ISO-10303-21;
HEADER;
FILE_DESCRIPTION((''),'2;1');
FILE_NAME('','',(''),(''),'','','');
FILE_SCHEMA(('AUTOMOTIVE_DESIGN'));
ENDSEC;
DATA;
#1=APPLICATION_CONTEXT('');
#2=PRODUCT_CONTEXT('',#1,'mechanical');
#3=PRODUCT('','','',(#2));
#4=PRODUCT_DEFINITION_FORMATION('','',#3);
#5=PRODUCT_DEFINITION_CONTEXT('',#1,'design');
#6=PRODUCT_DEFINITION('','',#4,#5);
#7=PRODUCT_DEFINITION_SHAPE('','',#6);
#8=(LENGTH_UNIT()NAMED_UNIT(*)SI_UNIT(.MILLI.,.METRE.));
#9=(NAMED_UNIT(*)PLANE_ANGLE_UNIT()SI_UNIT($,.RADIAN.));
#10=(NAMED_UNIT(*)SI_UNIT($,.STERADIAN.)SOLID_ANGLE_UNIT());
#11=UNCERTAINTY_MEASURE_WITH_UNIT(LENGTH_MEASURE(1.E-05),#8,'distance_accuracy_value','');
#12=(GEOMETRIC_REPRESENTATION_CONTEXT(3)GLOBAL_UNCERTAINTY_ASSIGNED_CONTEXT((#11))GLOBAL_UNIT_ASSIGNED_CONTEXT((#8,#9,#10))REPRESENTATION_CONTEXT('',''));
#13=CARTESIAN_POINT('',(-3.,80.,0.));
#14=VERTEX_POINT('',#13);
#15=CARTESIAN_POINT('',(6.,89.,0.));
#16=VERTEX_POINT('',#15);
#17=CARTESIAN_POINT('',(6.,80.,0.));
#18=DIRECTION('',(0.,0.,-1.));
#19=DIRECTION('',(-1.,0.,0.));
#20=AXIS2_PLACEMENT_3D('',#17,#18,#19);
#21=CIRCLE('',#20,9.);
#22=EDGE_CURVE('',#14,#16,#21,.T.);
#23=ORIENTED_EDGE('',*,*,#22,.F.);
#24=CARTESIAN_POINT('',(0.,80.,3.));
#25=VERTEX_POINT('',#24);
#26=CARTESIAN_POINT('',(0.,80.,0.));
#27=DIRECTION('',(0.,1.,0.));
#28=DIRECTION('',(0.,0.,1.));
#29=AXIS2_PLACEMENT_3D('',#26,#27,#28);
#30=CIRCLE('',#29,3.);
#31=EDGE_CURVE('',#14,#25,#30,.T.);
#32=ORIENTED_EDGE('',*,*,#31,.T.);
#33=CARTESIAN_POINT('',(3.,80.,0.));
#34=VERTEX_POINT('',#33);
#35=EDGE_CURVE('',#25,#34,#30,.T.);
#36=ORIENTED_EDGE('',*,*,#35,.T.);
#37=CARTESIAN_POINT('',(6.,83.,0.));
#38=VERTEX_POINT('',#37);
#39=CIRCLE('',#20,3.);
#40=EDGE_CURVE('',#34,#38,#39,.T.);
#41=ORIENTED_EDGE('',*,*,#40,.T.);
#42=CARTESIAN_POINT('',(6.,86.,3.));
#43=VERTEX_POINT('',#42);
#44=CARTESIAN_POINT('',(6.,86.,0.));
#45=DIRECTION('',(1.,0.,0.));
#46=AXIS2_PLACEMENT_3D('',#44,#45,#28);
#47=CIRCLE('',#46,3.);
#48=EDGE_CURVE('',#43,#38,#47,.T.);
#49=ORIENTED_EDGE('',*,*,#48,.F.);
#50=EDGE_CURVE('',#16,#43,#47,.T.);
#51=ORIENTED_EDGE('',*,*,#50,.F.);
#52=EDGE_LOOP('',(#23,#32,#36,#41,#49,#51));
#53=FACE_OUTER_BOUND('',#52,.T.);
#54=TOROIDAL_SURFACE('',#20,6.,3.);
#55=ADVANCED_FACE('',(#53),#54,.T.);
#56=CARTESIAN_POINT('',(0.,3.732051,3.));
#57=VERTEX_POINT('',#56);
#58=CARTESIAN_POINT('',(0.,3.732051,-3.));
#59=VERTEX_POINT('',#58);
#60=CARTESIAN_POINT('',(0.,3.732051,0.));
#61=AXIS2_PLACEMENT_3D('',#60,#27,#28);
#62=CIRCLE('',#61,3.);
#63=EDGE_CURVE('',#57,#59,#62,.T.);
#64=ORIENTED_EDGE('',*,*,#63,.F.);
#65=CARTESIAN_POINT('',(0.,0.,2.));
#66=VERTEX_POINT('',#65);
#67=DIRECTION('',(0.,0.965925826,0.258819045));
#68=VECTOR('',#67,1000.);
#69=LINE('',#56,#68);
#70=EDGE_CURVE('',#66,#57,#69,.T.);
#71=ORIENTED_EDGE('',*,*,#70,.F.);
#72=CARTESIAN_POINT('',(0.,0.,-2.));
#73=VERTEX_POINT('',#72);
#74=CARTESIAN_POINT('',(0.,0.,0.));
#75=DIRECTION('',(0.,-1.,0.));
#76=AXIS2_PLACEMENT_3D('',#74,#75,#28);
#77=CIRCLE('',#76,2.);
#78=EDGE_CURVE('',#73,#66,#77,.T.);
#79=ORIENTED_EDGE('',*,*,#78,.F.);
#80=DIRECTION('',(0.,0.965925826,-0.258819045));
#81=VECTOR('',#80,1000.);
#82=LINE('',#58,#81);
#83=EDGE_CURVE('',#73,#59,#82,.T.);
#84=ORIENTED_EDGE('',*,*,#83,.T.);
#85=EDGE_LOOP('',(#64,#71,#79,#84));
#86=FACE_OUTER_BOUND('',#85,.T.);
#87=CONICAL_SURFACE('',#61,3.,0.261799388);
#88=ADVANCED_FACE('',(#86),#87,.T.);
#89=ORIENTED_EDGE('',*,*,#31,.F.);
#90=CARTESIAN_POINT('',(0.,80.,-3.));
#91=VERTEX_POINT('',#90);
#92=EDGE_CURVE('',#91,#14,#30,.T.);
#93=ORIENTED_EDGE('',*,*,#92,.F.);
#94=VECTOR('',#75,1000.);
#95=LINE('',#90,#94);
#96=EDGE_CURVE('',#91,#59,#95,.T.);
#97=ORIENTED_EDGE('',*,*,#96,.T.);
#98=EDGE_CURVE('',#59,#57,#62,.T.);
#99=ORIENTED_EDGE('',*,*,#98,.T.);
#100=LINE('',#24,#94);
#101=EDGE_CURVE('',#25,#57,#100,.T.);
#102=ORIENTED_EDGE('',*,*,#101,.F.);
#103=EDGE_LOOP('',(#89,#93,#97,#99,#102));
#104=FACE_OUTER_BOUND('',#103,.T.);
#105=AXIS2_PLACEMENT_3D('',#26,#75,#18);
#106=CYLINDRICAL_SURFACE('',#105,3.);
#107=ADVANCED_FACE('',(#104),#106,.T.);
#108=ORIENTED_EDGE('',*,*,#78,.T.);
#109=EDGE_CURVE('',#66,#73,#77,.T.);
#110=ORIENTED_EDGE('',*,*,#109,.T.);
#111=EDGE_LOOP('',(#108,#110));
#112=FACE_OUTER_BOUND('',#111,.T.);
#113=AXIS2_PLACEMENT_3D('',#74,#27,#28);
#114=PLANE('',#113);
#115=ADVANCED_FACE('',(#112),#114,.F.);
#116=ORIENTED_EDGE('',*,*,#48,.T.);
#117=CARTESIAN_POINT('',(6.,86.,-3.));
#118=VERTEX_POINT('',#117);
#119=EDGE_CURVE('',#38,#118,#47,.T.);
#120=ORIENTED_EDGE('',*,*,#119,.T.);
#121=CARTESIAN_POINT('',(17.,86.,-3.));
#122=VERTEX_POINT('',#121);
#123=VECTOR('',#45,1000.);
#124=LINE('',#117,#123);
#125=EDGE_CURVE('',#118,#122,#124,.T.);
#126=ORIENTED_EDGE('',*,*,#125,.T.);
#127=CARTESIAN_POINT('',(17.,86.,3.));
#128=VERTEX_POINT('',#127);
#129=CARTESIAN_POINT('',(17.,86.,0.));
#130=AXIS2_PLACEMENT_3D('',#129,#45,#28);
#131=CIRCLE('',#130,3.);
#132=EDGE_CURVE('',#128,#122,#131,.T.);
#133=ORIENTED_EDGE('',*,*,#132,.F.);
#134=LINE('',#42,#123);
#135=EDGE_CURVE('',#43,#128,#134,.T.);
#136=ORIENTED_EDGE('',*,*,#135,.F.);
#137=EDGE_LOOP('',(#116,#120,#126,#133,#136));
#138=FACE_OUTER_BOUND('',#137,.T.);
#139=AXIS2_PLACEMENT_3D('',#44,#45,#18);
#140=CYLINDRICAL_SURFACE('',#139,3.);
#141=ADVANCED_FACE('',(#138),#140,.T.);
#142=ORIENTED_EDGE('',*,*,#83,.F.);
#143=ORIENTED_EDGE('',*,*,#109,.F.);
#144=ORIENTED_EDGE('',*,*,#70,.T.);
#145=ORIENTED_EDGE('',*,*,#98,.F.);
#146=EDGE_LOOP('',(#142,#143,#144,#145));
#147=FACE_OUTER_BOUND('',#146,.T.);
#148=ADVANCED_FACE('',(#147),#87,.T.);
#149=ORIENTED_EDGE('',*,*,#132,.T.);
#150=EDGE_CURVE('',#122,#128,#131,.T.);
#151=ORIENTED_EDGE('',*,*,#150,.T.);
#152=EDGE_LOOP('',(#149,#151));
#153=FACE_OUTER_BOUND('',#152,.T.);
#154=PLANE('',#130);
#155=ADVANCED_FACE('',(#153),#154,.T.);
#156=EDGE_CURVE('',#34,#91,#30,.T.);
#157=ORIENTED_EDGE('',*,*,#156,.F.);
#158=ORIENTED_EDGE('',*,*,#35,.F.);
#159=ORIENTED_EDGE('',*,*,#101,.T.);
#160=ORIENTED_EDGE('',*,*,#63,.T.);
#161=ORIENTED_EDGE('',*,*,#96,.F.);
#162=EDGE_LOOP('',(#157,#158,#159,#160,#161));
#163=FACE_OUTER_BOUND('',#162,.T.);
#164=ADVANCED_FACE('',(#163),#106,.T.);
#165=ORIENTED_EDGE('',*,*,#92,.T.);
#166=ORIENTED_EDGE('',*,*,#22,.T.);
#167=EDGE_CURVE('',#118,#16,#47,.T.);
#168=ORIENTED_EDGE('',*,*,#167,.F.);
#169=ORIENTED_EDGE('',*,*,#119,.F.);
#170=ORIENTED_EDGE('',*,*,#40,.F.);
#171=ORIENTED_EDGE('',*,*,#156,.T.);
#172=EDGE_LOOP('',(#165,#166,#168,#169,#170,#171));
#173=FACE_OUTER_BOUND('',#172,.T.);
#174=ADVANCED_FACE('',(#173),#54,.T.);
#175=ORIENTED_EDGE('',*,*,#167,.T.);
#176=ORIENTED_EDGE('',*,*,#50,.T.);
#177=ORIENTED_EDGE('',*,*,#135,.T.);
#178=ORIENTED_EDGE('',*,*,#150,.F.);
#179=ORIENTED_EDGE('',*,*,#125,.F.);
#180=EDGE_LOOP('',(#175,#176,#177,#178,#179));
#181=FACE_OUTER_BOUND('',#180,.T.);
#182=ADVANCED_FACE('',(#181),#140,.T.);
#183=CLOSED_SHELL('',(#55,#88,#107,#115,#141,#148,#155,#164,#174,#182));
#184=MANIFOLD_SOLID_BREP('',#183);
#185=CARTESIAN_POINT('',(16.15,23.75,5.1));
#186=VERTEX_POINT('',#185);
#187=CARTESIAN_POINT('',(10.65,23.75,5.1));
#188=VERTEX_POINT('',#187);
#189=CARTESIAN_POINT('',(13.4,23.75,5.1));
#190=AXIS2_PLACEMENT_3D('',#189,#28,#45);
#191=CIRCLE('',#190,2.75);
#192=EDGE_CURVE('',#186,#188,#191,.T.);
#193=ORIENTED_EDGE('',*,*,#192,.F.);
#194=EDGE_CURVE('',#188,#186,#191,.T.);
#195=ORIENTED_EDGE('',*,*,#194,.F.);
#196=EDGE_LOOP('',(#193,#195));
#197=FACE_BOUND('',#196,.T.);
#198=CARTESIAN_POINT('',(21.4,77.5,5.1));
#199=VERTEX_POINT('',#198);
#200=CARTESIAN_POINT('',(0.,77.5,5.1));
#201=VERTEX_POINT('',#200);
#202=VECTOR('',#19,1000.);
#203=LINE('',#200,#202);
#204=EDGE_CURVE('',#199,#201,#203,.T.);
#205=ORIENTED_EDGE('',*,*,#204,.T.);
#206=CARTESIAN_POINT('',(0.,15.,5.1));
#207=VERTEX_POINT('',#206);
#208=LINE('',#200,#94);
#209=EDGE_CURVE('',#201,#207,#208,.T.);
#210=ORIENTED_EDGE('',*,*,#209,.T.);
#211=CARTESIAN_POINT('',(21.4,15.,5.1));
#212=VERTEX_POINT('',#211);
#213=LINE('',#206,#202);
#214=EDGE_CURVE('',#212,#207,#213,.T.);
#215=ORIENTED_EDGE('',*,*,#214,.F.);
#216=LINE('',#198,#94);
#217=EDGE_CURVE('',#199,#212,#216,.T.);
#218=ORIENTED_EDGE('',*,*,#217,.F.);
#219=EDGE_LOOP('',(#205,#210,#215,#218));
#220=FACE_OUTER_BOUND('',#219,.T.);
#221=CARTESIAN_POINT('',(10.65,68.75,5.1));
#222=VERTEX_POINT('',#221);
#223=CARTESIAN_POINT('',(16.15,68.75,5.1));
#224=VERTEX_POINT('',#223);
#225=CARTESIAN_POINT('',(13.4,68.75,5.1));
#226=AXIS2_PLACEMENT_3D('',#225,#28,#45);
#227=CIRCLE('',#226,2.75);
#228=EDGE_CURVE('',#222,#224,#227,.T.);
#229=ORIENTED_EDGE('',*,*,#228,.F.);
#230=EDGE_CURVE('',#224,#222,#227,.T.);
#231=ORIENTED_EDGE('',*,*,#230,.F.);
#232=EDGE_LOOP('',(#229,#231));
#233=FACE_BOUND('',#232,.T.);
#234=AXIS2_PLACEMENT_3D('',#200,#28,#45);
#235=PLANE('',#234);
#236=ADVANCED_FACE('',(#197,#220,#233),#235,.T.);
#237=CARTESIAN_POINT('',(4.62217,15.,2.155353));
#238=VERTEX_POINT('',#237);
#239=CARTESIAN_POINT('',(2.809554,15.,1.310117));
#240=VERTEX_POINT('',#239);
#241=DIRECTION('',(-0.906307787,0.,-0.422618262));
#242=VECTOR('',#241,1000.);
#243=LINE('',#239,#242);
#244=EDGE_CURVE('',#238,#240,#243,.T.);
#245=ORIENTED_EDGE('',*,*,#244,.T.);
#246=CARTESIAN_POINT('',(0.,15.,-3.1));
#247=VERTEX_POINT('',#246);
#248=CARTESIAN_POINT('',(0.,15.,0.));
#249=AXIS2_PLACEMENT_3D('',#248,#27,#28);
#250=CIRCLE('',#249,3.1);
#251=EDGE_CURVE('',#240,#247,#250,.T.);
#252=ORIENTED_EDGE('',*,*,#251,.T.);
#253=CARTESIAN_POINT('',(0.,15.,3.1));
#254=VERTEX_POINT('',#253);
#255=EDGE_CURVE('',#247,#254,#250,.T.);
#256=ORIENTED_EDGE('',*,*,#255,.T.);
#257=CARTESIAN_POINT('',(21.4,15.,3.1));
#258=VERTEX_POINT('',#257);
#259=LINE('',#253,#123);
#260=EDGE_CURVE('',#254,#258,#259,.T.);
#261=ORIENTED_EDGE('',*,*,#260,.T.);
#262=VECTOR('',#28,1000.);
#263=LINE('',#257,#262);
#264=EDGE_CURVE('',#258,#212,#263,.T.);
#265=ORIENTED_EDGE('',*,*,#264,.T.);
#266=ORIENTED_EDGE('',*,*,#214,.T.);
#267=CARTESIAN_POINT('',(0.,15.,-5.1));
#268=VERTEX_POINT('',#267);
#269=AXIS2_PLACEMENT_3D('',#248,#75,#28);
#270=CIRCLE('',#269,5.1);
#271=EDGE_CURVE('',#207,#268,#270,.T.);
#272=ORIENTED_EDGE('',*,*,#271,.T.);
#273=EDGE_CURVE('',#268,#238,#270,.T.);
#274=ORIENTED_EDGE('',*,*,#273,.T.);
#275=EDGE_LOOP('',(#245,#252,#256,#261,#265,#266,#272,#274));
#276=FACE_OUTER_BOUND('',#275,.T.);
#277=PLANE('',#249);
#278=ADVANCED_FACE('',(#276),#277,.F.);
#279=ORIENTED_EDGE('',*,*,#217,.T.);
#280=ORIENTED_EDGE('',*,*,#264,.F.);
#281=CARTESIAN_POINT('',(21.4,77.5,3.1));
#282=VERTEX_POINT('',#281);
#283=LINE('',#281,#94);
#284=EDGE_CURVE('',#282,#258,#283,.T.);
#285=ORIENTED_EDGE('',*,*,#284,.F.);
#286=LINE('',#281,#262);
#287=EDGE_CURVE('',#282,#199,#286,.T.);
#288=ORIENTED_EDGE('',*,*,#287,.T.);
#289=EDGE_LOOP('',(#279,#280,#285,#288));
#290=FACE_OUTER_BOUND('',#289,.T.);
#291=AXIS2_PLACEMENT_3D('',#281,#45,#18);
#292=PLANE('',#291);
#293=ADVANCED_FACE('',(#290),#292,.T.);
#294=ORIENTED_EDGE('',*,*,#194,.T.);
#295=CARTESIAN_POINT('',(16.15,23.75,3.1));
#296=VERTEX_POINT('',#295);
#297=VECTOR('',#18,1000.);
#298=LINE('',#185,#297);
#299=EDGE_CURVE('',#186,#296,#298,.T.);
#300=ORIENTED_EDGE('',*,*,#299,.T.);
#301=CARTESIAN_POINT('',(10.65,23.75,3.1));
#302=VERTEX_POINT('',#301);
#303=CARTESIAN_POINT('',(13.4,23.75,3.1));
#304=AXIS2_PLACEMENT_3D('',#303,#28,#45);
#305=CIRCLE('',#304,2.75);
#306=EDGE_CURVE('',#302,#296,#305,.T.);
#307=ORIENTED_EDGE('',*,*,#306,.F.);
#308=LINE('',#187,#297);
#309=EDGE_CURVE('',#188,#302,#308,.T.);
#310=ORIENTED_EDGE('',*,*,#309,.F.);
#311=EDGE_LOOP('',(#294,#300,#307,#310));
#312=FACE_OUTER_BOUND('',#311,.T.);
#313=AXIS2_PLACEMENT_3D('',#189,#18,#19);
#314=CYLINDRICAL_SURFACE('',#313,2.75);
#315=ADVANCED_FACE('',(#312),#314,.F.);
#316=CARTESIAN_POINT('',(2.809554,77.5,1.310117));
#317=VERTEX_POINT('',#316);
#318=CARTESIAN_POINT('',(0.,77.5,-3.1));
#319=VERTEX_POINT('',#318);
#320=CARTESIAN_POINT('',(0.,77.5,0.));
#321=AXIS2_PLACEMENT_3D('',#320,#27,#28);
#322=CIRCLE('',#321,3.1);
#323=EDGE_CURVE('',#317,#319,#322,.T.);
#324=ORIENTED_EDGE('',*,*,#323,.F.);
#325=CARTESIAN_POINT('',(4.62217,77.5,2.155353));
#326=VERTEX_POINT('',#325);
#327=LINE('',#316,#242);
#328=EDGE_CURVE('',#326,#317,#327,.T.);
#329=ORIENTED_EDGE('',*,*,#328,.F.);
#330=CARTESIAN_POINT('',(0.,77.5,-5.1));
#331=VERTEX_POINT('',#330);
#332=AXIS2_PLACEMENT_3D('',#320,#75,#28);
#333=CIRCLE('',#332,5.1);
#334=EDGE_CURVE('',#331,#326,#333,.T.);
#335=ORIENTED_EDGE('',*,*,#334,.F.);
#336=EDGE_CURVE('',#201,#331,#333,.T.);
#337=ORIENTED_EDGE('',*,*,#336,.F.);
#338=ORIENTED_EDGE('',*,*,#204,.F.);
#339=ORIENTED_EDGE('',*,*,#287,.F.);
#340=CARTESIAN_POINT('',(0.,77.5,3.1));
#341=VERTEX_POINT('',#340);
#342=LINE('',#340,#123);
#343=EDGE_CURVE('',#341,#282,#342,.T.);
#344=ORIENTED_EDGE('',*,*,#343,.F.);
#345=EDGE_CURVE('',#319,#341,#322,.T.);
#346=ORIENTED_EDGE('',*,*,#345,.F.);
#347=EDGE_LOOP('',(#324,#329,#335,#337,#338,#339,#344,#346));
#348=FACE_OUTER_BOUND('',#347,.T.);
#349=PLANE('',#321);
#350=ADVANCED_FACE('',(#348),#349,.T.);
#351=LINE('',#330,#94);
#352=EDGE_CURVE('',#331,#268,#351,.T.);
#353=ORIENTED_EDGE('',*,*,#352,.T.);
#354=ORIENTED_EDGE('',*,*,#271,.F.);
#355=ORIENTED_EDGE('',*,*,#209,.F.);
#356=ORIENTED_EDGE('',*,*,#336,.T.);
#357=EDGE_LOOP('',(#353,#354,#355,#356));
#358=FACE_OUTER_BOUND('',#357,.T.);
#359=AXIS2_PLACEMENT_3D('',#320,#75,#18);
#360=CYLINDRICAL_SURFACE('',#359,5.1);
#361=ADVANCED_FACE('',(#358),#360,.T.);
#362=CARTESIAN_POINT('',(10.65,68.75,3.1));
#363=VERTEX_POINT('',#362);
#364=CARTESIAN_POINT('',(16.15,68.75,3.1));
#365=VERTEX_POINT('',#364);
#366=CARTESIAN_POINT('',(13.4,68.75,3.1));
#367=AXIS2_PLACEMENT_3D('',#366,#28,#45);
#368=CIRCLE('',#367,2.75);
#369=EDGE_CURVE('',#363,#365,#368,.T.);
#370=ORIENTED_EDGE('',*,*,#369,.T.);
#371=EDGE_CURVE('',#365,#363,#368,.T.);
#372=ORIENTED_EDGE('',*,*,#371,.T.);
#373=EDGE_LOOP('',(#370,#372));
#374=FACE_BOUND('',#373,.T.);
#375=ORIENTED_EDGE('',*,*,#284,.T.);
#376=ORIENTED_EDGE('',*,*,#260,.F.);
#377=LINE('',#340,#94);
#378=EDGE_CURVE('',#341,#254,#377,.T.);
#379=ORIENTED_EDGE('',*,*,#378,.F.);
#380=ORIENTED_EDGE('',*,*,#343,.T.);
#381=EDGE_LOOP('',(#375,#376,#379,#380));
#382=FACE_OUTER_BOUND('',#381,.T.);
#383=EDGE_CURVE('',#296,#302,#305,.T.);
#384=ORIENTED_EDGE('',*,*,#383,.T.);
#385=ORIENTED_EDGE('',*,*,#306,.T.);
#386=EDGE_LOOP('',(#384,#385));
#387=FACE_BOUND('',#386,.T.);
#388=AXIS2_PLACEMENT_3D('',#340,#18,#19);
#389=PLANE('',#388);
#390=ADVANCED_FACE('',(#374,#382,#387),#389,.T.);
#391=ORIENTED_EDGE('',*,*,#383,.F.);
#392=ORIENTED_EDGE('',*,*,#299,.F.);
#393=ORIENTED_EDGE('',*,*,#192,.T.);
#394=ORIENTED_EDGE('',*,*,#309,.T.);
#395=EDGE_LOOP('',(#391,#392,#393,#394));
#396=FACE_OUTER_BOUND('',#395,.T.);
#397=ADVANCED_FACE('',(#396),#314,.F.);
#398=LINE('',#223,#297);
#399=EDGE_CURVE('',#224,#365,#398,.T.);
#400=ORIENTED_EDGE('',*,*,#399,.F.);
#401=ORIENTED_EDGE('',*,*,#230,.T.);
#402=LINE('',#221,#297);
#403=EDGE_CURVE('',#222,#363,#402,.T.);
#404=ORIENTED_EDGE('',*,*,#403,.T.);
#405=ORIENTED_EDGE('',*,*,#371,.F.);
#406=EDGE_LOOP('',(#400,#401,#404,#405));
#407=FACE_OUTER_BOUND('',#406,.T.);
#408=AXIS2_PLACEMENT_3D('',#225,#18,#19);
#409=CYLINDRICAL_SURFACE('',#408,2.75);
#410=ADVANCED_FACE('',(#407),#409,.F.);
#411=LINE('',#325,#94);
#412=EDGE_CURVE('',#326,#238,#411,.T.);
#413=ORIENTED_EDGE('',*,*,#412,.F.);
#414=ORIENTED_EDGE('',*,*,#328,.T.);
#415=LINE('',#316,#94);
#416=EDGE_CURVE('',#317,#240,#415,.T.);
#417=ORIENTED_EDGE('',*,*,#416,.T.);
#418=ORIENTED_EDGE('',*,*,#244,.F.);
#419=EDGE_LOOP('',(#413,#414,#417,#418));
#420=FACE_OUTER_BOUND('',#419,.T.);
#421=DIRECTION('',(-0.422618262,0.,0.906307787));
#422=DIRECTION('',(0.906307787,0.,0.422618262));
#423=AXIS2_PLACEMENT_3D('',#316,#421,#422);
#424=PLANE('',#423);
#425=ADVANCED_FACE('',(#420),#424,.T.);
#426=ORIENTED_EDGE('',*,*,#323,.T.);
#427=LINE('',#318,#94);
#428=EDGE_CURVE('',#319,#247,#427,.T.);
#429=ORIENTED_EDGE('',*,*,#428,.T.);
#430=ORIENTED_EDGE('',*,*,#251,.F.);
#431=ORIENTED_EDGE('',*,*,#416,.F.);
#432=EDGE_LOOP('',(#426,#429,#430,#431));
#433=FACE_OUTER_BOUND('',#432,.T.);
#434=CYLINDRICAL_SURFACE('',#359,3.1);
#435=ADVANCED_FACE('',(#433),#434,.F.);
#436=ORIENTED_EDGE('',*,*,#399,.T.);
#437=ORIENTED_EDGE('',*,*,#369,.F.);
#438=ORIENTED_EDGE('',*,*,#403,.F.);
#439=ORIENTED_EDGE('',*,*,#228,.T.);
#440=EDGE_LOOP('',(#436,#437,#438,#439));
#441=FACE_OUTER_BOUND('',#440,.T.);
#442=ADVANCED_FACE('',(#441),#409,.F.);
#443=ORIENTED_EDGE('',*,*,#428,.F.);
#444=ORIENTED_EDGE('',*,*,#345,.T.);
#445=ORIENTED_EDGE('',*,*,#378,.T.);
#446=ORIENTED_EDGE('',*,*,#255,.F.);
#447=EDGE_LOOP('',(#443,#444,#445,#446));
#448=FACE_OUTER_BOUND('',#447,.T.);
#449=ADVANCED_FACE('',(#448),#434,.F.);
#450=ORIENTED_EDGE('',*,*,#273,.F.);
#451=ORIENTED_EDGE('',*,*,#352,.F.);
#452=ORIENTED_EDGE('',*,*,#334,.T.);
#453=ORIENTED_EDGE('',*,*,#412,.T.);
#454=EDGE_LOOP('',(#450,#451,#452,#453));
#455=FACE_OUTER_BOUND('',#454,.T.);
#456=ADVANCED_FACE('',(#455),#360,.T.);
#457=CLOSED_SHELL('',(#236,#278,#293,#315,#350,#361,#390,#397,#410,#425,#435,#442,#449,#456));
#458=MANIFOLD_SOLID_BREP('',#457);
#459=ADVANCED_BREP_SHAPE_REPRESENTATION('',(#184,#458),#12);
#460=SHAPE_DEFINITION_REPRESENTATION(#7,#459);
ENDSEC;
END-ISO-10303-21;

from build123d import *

# Parameters (mm, degrees)
SKETCH_2_R          = 3
EXTRUDE_1_DEPTH     = 62.5
SKETCH_5_R          = 2.75
CUT_EXTRUDE_2_DEPTH = 92.903210052
CHAMFER_1_SIZE      = 1
CHAMFER_1_SIZE2     = 3.732050808


with BuildPart() as part:
    # 扫描1: sweep along a path in 草图1
    with BuildLine(Plane.XY) as sweep_1_path:
        Line((0, 0), (0, 80))
        ThreePointArc((0, 80), (1.757359313, 84.242640687), (6, 86))
        Line((6, 86), (17, 86))
    # 草图2 → 扫描1 (sweep)
    with BuildSketch(Plane(origin=(0, 0, 0), x_dir=(1, 0, 0), z_dir=(0, 1, 0))):
        Circle(SKETCH_2_R)
    sweep(path=sweep_1_path.line)

    # 倒角1
    chamfer_1_edges = [part.edges().sort_by_distance(p)[0] for p in [
        (-3, 0, 0),
    ]]
    chamfer_1_side = [part.faces().sort_by_distance(p)[0] for p in [
        (0, 0, 0),
    ]]
    chamfer(chamfer_1_edges, length=CHAMFER_1_SIZE, length2=CHAMFER_1_SIZE2, reference=chamfer_1_side[0])


with BuildPart() as body_2:
    # 草图3 → 凸台-拉伸1 (new body)
    with BuildSketch(Plane(origin=(0, 15, 0), x_dir=(-1, 0, 0), z_dir=(0, -1, 0))):
        with BuildLine():
            Line((-21.4, -3.1), (-21.4, -5.1))
            Line((-21.4, -5.1), (0, -5.1))
            ThreePointArc((0, -5.1), (2.740228003, 4.301296374), (-4.622169714, -2.155353135))
            Line((-4.622169714, -2.155353135), (-2.80955414, -1.310116611))
            ThreePointArc((-2.80955414, -1.310116611), (1.665628786, 2.614513482), (0, -3.1))
            Line((0, -3.1), (-21.4, -3.1))
        make_face()
    extrude(amount=-EXTRUDE_1_DEPTH)

    # 草图5 → 切除-拉伸2 (cut, through all)
    with BuildSketch(Plane.XY.offset(3.1)):
        with Locations((13.4, 23.75)):
            Circle(SKETCH_5_R)
        with Locations((13.4, 68.75)):
            Circle(SKETCH_5_R)
    extrude(amount=CUT_EXTRUDE_2_DEPTH, mode=Mode.SUBTRACT)


solid = Compound([part.part, body_2.part])
